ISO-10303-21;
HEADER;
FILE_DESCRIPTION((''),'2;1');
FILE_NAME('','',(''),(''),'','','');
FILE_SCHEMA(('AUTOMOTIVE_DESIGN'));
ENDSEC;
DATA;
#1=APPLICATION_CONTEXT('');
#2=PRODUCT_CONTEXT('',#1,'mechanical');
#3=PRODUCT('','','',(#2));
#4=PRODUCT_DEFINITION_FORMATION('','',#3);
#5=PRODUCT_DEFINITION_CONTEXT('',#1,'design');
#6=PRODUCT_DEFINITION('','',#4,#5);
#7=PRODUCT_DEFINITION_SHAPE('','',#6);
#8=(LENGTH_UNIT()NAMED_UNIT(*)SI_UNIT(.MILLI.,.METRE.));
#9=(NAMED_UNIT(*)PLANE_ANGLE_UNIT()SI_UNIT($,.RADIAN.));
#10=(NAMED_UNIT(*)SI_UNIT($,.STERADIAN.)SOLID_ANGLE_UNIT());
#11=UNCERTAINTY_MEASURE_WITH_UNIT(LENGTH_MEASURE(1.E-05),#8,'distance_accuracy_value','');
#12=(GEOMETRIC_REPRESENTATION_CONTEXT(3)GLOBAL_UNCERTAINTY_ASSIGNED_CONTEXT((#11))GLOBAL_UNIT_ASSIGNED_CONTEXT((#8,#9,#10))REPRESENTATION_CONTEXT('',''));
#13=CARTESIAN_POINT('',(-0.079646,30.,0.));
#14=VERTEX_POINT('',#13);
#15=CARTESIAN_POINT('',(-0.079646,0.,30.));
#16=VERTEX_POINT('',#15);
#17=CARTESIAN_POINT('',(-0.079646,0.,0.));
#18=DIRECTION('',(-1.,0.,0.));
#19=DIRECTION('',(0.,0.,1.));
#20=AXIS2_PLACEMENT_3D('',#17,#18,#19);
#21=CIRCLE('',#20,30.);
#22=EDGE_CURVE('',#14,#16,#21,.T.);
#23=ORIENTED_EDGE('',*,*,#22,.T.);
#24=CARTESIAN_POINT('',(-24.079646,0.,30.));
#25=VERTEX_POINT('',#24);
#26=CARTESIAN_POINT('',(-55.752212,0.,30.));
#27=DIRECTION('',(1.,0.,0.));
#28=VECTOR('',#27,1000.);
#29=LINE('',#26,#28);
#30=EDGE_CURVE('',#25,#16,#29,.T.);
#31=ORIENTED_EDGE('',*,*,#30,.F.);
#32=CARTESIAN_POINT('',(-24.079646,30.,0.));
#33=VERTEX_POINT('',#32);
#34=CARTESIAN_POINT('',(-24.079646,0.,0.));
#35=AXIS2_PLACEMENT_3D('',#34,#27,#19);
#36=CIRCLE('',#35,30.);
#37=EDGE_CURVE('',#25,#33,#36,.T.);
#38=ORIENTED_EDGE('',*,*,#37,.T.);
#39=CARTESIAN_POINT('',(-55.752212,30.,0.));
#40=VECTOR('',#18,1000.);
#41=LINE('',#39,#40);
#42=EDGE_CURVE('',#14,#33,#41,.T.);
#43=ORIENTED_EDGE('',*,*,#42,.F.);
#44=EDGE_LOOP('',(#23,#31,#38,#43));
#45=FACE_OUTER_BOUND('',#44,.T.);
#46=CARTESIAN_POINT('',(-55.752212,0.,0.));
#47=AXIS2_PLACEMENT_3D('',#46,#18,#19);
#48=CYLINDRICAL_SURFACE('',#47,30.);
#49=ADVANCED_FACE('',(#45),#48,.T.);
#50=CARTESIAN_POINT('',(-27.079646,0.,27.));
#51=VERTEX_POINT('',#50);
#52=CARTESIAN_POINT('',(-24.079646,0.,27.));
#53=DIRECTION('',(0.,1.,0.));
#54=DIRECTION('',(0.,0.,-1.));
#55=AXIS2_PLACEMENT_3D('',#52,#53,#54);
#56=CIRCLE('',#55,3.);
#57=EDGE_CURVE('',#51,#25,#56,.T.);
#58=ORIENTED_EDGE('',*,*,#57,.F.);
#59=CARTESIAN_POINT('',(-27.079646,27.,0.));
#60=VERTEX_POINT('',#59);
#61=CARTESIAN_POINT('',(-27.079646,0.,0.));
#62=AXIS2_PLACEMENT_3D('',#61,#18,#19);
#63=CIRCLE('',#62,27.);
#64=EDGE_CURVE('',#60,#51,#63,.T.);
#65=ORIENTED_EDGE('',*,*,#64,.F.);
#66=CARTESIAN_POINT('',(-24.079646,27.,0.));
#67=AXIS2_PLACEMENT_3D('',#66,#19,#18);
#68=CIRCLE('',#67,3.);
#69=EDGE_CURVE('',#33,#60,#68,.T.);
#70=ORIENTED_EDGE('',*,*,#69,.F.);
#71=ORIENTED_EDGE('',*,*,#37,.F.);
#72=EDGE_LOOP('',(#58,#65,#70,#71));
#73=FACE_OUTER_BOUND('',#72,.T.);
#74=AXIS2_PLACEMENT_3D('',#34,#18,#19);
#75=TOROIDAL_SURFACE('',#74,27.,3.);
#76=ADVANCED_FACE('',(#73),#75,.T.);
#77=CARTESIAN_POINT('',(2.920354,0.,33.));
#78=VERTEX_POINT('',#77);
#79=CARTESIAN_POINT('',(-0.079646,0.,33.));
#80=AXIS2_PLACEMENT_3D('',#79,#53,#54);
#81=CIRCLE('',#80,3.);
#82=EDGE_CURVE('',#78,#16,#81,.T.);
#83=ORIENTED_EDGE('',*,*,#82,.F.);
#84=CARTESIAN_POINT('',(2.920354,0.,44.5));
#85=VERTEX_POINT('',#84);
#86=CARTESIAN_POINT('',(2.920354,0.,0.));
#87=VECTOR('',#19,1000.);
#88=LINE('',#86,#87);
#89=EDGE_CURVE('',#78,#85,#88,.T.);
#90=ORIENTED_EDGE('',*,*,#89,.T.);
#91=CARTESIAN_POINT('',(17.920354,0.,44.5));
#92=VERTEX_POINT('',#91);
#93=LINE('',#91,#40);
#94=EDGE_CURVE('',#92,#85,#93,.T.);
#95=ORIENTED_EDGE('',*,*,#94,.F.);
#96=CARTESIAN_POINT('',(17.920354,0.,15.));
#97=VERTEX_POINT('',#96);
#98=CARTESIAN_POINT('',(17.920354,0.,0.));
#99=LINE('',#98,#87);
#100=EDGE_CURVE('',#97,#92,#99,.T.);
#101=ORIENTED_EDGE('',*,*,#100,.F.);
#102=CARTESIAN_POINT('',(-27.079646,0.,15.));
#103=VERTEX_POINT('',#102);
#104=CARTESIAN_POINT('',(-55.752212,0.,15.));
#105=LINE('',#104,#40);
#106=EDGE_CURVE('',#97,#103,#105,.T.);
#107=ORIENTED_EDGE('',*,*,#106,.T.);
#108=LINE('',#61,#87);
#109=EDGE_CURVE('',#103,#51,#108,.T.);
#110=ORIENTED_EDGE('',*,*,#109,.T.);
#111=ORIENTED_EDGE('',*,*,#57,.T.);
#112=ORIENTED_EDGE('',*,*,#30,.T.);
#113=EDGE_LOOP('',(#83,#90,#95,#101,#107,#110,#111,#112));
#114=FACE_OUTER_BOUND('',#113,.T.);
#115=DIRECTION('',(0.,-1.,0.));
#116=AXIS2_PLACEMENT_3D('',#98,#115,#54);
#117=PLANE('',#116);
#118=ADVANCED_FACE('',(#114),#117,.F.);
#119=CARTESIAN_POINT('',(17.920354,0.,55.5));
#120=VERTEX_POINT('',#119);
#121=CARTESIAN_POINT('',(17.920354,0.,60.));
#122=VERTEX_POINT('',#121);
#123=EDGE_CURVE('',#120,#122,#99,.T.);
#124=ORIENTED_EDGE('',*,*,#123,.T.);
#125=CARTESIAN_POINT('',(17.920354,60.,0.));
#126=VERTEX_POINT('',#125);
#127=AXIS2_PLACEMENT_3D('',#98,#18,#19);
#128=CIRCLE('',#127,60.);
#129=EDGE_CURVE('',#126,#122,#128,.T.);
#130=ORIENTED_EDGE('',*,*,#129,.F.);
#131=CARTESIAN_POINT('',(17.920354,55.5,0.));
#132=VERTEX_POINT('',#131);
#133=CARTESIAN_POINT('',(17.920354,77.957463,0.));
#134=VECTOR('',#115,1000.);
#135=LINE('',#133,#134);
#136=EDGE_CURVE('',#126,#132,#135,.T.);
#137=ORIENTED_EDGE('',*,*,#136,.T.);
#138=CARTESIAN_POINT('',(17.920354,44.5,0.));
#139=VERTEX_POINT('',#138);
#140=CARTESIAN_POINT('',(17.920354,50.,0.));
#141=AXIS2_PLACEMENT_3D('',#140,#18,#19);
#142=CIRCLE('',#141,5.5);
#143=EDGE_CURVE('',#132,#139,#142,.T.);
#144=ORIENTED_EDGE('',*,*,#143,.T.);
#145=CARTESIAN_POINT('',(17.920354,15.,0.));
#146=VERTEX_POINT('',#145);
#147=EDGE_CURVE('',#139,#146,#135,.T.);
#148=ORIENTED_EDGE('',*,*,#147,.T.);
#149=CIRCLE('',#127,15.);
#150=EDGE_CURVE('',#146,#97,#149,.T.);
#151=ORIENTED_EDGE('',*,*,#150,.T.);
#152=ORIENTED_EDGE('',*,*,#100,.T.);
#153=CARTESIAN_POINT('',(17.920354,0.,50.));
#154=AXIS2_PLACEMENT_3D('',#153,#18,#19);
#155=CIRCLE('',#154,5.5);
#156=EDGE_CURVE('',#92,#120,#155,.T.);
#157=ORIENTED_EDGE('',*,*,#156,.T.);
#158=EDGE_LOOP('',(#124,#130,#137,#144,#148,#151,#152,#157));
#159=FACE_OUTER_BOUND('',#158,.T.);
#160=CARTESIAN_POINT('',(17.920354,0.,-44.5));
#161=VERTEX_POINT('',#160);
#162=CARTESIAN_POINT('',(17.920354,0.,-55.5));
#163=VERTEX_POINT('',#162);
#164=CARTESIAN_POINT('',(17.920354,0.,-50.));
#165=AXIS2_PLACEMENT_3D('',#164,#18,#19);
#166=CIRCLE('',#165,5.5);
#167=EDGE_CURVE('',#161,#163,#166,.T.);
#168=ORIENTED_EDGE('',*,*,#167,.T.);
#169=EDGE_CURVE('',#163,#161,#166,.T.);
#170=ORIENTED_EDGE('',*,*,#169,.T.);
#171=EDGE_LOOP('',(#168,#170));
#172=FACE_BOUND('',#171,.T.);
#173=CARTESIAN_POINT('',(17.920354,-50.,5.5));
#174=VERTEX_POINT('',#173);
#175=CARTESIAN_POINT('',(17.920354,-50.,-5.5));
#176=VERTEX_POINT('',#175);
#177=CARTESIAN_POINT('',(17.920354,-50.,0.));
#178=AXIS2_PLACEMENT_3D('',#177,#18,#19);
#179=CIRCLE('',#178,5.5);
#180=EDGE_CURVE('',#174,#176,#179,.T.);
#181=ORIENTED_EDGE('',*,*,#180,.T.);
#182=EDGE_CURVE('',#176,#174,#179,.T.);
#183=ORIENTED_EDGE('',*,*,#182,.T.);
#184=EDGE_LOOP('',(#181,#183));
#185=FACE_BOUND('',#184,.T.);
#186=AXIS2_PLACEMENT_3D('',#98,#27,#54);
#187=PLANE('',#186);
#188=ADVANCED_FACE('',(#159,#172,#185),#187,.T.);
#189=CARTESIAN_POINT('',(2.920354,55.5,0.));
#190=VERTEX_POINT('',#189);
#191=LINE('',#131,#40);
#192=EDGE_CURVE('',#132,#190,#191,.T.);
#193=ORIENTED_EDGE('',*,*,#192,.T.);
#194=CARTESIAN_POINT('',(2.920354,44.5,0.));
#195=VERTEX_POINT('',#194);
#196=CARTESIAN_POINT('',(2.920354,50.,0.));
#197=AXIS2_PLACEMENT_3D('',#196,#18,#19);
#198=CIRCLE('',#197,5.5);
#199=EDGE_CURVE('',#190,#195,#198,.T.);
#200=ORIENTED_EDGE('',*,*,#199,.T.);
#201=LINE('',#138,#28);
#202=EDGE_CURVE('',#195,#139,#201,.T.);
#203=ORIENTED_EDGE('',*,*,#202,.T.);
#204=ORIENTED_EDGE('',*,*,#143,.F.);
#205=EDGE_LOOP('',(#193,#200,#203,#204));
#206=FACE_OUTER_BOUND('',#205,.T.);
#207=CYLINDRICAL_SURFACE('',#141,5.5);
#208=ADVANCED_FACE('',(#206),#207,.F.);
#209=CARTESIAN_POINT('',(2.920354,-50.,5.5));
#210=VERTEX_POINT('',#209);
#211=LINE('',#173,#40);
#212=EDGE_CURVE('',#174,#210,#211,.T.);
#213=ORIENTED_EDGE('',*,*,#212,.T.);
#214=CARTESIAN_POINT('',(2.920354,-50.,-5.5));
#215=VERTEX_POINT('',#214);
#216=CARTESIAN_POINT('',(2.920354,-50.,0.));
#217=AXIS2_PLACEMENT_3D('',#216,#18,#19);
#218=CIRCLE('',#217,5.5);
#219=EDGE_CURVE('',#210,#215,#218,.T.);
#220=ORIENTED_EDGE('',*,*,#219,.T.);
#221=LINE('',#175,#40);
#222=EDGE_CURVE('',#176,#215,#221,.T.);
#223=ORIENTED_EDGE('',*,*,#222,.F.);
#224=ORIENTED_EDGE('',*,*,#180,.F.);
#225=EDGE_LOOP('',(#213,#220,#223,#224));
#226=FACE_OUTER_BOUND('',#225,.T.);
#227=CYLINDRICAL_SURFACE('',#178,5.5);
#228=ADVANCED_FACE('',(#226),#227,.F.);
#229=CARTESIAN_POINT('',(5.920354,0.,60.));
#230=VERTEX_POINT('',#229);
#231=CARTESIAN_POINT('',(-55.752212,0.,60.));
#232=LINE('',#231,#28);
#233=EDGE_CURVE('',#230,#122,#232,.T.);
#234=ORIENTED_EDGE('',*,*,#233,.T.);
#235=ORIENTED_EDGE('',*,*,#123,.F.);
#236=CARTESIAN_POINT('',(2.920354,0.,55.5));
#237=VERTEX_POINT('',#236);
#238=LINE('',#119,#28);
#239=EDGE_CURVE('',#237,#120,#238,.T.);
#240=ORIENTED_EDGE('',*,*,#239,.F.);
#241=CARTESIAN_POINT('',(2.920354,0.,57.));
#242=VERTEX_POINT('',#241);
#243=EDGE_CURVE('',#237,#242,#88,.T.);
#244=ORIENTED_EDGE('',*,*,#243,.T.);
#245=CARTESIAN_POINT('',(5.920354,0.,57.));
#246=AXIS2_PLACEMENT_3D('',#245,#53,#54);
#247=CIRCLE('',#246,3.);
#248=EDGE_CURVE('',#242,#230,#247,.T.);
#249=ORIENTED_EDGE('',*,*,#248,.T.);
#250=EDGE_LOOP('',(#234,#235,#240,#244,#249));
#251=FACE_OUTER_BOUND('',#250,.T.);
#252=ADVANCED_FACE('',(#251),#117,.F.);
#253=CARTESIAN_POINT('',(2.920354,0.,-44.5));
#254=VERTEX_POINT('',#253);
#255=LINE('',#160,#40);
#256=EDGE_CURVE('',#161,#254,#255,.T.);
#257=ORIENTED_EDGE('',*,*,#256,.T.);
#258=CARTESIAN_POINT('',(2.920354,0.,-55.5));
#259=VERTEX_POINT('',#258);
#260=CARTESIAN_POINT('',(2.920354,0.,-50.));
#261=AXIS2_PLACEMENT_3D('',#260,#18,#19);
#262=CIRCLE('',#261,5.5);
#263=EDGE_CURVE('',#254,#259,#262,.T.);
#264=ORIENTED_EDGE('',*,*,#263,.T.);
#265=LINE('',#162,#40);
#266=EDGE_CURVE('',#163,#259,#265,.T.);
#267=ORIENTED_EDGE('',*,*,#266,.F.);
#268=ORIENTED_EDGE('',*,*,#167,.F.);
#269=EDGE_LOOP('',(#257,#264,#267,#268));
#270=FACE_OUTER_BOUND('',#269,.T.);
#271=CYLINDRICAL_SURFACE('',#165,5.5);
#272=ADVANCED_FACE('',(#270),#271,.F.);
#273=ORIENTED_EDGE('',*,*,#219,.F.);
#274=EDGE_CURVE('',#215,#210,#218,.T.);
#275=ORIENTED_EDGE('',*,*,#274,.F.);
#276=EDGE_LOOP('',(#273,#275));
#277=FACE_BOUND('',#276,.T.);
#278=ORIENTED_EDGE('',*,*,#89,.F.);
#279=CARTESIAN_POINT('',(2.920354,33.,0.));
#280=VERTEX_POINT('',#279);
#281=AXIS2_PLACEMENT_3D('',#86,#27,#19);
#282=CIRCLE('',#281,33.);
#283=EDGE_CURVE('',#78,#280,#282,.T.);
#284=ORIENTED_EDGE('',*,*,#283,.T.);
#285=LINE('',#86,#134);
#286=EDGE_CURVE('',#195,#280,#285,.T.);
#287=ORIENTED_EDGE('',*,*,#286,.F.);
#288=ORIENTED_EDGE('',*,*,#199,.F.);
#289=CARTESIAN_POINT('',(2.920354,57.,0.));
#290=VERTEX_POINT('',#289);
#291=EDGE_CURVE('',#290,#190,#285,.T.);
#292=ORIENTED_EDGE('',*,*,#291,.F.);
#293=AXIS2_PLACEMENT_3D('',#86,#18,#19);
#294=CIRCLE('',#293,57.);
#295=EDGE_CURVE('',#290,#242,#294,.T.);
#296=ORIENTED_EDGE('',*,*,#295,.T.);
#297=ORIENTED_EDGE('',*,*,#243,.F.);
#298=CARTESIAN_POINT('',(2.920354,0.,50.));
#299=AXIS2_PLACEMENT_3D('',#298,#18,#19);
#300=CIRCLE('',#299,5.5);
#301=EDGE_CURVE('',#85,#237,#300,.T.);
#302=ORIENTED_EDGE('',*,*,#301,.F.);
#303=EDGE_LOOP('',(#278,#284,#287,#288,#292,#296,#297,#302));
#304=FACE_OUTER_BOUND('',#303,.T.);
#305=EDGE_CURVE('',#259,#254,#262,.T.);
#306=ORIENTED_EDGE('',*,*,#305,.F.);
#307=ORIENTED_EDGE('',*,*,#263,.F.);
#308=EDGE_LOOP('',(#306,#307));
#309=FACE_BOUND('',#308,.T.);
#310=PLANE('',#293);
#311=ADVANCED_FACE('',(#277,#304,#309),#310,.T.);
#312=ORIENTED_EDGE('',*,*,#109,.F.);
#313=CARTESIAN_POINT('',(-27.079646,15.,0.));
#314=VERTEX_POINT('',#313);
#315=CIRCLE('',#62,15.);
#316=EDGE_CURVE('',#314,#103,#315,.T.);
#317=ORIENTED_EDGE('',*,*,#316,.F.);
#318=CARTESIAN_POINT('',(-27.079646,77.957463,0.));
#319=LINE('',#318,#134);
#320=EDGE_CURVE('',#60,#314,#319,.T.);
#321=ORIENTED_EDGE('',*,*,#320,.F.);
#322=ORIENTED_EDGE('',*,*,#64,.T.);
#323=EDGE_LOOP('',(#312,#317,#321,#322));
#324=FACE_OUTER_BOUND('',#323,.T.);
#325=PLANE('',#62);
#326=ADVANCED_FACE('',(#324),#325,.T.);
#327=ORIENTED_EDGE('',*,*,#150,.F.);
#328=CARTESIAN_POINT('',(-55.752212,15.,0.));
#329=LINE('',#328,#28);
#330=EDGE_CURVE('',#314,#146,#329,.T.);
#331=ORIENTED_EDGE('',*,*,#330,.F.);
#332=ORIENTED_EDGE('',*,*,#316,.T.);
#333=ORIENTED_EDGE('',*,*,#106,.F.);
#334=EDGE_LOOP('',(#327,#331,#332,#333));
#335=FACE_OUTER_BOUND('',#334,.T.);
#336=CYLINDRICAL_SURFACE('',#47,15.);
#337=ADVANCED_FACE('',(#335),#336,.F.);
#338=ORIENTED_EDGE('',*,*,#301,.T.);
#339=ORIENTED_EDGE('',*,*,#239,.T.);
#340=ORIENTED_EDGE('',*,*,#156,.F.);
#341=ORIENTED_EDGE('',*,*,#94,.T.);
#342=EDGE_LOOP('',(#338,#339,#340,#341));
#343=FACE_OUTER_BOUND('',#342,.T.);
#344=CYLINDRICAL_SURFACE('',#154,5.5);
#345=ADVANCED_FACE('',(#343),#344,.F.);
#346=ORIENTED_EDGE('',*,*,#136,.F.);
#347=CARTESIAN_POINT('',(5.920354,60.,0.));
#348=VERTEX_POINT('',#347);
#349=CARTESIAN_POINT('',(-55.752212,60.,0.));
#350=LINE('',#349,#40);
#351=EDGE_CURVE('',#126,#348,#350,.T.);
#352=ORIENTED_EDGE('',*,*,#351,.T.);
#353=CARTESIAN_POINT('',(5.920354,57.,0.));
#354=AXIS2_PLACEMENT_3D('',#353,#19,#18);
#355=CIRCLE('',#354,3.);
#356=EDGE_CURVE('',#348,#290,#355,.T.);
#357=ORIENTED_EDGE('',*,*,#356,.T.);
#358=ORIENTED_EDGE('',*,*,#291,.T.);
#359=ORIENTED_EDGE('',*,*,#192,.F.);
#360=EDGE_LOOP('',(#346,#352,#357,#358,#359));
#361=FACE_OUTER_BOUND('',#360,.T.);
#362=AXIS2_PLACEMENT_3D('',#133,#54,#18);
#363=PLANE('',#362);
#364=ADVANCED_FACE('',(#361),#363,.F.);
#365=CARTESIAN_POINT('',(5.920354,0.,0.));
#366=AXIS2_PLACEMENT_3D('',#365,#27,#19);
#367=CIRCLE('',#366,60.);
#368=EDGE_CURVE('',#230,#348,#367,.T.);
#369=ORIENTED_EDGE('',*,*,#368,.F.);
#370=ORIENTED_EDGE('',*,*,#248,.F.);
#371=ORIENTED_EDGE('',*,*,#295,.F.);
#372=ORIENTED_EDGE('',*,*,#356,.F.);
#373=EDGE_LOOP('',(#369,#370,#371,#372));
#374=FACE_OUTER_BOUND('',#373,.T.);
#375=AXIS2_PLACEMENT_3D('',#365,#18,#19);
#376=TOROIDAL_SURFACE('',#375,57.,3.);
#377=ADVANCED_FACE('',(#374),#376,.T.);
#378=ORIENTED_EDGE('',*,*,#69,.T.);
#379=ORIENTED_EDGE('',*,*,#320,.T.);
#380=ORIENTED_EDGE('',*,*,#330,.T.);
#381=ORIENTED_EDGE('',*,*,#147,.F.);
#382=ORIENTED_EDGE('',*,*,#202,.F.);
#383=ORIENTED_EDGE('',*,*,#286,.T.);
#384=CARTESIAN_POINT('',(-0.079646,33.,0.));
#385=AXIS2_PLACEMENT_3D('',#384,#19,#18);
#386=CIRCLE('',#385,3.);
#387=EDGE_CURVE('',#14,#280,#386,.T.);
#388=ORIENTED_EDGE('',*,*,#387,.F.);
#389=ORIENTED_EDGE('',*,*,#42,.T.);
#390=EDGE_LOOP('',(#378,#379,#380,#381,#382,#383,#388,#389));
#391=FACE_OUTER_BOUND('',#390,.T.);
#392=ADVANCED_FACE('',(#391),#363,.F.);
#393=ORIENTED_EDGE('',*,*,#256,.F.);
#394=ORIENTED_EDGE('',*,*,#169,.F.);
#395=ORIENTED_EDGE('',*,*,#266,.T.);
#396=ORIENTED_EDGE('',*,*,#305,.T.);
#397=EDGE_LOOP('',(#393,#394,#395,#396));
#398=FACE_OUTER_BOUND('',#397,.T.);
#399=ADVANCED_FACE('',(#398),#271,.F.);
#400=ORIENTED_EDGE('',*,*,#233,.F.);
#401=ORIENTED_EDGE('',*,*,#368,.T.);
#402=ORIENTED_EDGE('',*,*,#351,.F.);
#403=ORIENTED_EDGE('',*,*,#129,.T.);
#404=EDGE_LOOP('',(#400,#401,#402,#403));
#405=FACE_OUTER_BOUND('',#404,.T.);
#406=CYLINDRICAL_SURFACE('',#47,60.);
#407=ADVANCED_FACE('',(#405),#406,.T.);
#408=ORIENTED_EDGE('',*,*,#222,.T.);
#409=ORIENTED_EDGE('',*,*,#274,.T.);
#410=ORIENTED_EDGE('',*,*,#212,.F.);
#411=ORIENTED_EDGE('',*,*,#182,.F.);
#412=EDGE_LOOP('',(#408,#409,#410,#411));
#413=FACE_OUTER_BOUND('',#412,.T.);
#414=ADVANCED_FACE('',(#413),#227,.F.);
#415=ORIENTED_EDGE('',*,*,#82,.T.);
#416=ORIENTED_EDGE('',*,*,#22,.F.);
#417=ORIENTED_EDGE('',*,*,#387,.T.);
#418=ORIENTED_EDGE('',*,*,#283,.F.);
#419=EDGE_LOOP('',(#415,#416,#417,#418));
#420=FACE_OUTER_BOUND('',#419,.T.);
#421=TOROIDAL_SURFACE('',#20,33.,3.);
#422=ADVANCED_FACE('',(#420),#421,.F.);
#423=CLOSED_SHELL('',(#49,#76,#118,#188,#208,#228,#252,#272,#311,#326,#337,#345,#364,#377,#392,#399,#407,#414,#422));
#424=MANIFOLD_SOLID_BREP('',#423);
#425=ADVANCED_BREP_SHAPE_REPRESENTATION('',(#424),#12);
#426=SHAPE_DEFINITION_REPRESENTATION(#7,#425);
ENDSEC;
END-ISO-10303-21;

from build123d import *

# Parameters (mm, degrees)
BOLT_HOLES_SKETCH_R = 5.5
BOLT_HOLES_11_DEPTH = 91
EDGE_FILLET_R3_R    = 3
SIDE_CUTOUT_DEPTH   = 97.046863624


with BuildPart() as part:
    # Bed Profile Sketch → Bed Body Revolve (revolve)
    with BuildSketch(Plane.XY, mode=Mode.PRIVATE) as bed_body_revolve_sk:
        Polygon((17.920353982, 15), (17.920353982, 60), (2.920353982, 60), (2.920353982, 30), (-27.079646018, 30), (-27.079646018, 15), align=None)
    revolve(bed_body_revolve_sk.sketch.rotate(Axis((-55.752212389, 0, 0), (1, 0, 0)), 90), axis=Axis((-55.752212389, 0, 0), (1, 0, 0)))

    # Bolt Holes Sketch → Bolt Holes Ø11 (cut, through all)
    with BuildSketch(Plane.ZY.offset(-2.920353982)):
        with Locations((0, 50)):
            Circle(BOLT_HOLES_SKETCH_R)
        with Locations((50, 0)):
            Circle(BOLT_HOLES_SKETCH_R)
        with Locations((0, -50)):
            Circle(BOLT_HOLES_SKETCH_R)
        with Locations((-50, 0)):
            Circle(BOLT_HOLES_SKETCH_R)
    extrude(amount=-BOLT_HOLES_11_DEPTH, mode=Mode.SUBTRACT)

    # Edge Fillet R3
    edge_fillet_r3_edges = [part.edges().sort_by_distance(p)[0] for p in [
        (-27.079646018, 0, -30),
        (2.920353982, 0, -30),
        (2.920353982, 0, -60),
    ]]
    fillet(edge_fillet_r3_edges, radius=EDGE_FILLET_R3_R)

    # Side Cutout Sketch → Side Cutout (cut, through all)
    with BuildSketch(Plane.ZY.offset(27.079646018)):
        with BuildLine():
            Line((0, 77.957463499), (0, 0))
            Line((0, 0), (74.222252728, 0))
            ThreePointArc((74.222252728, 0), (53.256645699, 54.350663604), (0, 77.957463499))
        make_face()
    extrude(amount=-SIDE_CUTOUT_DEPTH, mode=Mode.SUBTRACT)


solid = part.part
